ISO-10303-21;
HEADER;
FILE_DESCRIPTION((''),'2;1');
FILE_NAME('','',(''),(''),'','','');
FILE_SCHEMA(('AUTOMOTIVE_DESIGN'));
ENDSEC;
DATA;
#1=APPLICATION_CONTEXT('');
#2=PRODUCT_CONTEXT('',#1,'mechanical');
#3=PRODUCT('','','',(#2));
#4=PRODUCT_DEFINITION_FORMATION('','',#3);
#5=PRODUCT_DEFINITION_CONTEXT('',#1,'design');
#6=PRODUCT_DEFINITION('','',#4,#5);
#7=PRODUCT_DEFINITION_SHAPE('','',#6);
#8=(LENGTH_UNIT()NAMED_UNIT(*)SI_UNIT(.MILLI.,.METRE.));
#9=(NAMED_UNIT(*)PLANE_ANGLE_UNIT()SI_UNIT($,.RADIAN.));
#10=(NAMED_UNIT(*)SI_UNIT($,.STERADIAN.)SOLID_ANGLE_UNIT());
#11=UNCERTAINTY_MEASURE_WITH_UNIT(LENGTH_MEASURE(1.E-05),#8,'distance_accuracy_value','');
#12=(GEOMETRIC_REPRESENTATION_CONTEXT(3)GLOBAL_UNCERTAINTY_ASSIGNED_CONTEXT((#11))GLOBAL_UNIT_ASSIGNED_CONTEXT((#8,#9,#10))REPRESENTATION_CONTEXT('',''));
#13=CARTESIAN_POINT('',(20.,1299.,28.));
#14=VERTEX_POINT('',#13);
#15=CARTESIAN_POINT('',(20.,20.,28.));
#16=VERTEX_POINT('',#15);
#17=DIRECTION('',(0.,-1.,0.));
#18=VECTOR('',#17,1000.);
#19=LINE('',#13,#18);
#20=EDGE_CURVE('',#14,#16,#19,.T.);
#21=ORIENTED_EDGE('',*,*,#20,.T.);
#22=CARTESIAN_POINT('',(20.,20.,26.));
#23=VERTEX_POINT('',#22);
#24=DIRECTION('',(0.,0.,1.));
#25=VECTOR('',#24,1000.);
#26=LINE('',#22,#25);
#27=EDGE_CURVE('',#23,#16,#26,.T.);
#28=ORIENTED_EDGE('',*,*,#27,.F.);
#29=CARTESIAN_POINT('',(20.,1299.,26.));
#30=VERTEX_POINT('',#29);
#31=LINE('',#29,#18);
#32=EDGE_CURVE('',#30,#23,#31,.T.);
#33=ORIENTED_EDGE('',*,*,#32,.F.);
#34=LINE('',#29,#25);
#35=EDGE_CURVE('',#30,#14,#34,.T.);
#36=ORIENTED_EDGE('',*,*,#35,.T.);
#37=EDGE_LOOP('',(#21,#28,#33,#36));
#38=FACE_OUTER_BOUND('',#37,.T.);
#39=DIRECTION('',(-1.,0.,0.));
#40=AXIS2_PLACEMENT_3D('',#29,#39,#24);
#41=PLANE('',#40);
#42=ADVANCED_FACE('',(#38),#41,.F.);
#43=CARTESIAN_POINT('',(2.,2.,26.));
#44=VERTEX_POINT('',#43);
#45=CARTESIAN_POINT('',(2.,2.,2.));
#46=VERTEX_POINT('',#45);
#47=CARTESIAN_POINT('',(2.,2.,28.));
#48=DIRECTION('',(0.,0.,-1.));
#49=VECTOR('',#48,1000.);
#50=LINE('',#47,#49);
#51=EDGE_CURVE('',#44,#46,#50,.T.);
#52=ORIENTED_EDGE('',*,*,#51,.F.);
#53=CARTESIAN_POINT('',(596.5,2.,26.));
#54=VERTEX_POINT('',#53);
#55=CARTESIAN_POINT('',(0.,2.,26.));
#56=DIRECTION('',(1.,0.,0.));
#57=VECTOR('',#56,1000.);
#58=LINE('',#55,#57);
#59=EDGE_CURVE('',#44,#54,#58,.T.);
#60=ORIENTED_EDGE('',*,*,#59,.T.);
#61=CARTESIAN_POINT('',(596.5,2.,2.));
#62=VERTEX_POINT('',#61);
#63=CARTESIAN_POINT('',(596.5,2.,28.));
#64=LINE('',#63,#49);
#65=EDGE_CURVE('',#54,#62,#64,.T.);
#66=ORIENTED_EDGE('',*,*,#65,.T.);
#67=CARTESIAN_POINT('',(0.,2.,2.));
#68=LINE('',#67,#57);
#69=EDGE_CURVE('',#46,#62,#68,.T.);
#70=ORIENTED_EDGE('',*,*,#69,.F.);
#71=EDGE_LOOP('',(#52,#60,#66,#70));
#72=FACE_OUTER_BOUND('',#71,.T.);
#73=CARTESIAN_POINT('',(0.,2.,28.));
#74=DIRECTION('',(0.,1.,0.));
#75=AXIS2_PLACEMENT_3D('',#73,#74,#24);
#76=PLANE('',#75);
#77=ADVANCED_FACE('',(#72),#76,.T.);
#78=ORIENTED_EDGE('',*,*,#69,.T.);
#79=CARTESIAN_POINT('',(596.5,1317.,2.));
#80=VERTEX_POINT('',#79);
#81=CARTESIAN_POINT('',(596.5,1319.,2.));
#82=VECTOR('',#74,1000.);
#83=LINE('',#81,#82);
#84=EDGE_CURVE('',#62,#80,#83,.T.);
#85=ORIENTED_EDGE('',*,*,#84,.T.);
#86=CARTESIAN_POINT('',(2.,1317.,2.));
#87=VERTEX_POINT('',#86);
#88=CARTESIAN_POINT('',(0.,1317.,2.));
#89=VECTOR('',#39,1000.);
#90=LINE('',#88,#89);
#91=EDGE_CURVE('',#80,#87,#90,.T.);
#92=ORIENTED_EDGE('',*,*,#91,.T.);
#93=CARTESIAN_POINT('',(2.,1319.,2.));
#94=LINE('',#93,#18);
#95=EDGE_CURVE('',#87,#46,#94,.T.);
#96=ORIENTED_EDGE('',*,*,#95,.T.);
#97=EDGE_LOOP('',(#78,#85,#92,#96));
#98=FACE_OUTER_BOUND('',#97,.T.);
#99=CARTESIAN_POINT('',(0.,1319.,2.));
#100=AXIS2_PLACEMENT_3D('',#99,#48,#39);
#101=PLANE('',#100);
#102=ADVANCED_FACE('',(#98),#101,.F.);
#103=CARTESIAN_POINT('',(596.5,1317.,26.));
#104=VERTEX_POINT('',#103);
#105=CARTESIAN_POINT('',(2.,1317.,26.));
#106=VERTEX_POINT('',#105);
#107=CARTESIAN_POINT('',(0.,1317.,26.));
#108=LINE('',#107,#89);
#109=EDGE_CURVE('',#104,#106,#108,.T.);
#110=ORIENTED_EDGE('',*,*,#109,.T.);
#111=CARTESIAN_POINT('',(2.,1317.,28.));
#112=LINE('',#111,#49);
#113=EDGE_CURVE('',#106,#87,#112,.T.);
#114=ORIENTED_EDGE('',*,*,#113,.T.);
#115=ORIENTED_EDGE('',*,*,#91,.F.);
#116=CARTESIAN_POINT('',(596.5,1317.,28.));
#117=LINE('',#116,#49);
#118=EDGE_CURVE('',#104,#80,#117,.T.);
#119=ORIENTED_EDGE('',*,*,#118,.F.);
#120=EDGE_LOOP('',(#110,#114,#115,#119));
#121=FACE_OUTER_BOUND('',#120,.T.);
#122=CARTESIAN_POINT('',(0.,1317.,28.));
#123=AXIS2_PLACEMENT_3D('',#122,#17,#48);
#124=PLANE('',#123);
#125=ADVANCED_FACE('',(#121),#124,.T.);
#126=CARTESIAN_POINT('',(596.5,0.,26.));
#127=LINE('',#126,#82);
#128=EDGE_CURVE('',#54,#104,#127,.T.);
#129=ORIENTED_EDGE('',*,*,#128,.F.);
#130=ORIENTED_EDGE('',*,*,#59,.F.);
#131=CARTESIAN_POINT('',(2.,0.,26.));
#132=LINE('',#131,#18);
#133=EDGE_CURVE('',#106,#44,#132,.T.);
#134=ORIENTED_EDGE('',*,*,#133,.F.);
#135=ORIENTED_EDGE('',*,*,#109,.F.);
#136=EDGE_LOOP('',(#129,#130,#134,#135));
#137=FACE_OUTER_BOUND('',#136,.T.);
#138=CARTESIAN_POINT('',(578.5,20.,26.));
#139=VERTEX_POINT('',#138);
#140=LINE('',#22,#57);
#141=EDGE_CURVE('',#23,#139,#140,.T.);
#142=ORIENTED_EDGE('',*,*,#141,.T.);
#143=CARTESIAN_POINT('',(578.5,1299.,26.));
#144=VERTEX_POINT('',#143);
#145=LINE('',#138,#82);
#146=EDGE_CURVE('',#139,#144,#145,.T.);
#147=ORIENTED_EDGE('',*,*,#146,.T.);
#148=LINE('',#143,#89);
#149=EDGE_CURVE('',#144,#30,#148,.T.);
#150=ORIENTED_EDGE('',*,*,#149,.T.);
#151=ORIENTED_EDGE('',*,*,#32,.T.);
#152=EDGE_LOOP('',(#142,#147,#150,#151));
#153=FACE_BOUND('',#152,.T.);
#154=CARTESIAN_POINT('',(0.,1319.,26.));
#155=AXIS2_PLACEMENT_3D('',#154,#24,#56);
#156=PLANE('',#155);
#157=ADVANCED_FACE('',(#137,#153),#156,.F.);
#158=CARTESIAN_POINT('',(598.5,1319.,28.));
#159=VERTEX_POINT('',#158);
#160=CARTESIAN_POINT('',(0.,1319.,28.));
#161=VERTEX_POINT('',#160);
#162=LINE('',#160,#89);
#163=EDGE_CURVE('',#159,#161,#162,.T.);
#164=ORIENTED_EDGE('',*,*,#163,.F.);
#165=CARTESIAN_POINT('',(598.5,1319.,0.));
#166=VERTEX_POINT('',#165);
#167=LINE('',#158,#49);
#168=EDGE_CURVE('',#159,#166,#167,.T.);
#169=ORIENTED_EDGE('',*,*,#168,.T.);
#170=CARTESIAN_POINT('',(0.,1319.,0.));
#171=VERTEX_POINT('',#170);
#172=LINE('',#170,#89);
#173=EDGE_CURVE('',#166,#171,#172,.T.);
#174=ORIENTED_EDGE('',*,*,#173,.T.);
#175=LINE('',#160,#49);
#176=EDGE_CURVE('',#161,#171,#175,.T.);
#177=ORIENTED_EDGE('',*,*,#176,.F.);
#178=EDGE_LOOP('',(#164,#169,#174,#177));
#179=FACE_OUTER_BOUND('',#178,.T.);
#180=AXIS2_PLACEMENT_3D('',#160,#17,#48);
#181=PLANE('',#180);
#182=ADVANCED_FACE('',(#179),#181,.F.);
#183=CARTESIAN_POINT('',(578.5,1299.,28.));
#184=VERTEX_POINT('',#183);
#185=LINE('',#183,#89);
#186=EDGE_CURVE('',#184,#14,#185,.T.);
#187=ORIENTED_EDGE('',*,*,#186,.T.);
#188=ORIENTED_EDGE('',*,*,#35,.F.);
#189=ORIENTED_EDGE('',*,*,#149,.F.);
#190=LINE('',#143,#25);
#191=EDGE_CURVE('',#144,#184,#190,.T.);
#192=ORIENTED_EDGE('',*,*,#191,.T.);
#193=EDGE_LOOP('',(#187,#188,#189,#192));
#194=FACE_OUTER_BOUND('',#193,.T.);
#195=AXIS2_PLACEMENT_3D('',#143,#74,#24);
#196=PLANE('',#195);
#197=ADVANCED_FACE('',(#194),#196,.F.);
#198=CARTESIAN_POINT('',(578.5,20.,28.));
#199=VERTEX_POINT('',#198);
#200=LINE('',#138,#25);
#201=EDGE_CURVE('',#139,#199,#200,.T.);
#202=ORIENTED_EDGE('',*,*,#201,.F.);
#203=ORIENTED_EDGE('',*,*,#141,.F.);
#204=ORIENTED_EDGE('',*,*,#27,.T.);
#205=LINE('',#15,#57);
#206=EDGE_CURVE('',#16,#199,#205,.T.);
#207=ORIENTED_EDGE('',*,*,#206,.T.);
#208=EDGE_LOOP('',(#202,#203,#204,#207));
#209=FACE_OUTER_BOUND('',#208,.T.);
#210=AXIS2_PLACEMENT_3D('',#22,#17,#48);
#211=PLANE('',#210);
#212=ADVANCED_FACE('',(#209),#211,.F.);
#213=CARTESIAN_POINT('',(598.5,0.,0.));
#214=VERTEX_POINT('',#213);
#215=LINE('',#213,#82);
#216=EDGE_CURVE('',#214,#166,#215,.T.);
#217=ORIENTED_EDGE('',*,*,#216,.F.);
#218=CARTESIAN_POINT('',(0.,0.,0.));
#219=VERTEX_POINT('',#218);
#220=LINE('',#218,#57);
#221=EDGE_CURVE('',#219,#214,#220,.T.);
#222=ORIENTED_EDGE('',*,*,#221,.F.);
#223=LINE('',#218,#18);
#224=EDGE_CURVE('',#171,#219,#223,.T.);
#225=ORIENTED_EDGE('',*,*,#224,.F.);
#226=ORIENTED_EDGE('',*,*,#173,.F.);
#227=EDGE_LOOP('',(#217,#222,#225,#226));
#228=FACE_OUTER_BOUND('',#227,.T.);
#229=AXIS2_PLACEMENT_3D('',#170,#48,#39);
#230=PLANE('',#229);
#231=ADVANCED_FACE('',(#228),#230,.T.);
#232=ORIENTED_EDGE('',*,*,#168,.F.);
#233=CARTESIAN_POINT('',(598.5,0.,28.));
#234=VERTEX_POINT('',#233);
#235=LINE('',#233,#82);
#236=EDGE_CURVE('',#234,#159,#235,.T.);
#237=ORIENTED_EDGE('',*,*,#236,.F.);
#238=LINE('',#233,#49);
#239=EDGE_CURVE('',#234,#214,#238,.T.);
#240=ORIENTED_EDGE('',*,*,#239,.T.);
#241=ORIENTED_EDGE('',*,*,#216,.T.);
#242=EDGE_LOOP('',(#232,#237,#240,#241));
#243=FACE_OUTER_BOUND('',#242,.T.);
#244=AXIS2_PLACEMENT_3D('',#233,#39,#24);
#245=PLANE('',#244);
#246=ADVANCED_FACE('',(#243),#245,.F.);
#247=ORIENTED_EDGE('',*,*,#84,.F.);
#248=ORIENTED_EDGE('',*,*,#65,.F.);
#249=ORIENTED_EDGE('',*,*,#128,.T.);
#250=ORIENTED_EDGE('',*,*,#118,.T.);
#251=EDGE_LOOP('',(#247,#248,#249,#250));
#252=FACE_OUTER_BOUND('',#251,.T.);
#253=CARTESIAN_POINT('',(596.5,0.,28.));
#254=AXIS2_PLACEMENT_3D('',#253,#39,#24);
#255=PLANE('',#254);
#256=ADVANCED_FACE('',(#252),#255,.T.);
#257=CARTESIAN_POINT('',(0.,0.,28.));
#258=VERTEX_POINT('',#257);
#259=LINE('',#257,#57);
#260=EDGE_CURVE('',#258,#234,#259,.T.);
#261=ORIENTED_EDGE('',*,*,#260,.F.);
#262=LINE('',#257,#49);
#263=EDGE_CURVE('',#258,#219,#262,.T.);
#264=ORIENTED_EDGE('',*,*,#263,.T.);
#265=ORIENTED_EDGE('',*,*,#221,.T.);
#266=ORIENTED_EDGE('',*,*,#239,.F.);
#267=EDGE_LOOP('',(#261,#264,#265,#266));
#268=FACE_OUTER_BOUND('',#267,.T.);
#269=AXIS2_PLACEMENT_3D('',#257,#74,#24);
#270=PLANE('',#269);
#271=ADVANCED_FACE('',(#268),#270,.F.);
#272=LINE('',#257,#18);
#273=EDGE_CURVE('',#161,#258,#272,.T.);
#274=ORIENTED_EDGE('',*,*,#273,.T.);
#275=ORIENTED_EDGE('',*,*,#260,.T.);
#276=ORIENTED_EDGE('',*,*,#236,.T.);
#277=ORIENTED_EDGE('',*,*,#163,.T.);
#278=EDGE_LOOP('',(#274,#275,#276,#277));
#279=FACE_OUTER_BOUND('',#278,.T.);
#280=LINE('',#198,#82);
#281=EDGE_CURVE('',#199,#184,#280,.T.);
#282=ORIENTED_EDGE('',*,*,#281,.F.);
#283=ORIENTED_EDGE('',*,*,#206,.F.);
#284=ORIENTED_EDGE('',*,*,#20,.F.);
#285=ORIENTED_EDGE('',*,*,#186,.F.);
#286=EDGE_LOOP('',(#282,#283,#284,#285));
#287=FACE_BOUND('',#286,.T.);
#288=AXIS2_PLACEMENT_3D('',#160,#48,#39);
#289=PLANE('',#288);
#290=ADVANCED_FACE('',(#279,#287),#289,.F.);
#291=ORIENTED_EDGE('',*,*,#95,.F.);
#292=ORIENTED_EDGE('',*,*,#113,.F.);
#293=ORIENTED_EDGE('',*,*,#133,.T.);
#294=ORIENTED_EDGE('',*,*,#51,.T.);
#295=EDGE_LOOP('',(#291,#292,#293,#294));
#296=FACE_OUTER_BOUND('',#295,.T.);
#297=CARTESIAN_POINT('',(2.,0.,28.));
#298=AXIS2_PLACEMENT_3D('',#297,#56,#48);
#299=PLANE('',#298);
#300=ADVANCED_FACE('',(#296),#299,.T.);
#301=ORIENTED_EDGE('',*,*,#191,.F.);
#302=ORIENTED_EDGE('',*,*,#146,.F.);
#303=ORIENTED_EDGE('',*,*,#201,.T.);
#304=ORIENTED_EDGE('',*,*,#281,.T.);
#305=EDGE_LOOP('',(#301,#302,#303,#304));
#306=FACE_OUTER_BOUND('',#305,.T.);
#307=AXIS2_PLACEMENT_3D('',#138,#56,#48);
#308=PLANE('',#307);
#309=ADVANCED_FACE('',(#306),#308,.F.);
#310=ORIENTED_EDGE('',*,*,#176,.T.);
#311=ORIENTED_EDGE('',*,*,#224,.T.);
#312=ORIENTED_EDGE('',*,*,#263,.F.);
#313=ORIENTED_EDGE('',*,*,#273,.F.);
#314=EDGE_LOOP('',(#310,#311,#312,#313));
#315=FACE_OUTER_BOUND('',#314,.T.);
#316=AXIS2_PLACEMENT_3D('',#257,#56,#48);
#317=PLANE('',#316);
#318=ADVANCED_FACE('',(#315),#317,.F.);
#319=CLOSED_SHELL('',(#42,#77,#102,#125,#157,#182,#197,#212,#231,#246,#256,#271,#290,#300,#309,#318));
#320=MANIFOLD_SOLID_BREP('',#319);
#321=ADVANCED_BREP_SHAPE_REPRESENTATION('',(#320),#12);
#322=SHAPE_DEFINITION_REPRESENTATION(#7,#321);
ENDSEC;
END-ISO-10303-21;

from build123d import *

# Parameters (mm, degrees)
SKETCH_1_W      = 598.5
SKETCH_1_H      = 1319
EXTRUDE_1_DEPTH = 28
SHELL_1_T       = -2
SKETCH_2_W      = 598.5
SKETCH_2_H      = 1319
SKETCH_2_W_2    = 558.5
SKETCH_2_H_2    = 1279
EXTRUDE_2_DEPTH = 2


with BuildPart() as part:
    # 草图1 → 凸台-拉伸1 (new body)
    with BuildSketch(Plane.XY):
        with Locations((299.25, 659.5)):
            Rectangle(SKETCH_1_W, SKETCH_1_H)
    extrude(amount=EXTRUDE_1_DEPTH)

    # 抽壳1
    shell_1_openings = [part.faces().sort_by_distance(p)[0] for p in [
        (299.25, 659.5, 28),
    ]]
    offset(amount=SHELL_1_T, openings=shell_1_openings, kind=Kind.INTERSECTION)

    # 草图2 → 凸台-拉伸2 (add)
    with BuildSketch(Plane.XY.offset(28)):
        with Locations((299.25, 659.5)):
            Rectangle(SKETCH_2_W, SKETCH_2_H)
        with Locations((299.25, 659.5)):
            Rectangle(SKETCH_2_W_2, SKETCH_2_H_2, mode=Mode.SUBTRACT)
    extrude(amount=-EXTRUDE_2_DEPTH)


solid = part.part
